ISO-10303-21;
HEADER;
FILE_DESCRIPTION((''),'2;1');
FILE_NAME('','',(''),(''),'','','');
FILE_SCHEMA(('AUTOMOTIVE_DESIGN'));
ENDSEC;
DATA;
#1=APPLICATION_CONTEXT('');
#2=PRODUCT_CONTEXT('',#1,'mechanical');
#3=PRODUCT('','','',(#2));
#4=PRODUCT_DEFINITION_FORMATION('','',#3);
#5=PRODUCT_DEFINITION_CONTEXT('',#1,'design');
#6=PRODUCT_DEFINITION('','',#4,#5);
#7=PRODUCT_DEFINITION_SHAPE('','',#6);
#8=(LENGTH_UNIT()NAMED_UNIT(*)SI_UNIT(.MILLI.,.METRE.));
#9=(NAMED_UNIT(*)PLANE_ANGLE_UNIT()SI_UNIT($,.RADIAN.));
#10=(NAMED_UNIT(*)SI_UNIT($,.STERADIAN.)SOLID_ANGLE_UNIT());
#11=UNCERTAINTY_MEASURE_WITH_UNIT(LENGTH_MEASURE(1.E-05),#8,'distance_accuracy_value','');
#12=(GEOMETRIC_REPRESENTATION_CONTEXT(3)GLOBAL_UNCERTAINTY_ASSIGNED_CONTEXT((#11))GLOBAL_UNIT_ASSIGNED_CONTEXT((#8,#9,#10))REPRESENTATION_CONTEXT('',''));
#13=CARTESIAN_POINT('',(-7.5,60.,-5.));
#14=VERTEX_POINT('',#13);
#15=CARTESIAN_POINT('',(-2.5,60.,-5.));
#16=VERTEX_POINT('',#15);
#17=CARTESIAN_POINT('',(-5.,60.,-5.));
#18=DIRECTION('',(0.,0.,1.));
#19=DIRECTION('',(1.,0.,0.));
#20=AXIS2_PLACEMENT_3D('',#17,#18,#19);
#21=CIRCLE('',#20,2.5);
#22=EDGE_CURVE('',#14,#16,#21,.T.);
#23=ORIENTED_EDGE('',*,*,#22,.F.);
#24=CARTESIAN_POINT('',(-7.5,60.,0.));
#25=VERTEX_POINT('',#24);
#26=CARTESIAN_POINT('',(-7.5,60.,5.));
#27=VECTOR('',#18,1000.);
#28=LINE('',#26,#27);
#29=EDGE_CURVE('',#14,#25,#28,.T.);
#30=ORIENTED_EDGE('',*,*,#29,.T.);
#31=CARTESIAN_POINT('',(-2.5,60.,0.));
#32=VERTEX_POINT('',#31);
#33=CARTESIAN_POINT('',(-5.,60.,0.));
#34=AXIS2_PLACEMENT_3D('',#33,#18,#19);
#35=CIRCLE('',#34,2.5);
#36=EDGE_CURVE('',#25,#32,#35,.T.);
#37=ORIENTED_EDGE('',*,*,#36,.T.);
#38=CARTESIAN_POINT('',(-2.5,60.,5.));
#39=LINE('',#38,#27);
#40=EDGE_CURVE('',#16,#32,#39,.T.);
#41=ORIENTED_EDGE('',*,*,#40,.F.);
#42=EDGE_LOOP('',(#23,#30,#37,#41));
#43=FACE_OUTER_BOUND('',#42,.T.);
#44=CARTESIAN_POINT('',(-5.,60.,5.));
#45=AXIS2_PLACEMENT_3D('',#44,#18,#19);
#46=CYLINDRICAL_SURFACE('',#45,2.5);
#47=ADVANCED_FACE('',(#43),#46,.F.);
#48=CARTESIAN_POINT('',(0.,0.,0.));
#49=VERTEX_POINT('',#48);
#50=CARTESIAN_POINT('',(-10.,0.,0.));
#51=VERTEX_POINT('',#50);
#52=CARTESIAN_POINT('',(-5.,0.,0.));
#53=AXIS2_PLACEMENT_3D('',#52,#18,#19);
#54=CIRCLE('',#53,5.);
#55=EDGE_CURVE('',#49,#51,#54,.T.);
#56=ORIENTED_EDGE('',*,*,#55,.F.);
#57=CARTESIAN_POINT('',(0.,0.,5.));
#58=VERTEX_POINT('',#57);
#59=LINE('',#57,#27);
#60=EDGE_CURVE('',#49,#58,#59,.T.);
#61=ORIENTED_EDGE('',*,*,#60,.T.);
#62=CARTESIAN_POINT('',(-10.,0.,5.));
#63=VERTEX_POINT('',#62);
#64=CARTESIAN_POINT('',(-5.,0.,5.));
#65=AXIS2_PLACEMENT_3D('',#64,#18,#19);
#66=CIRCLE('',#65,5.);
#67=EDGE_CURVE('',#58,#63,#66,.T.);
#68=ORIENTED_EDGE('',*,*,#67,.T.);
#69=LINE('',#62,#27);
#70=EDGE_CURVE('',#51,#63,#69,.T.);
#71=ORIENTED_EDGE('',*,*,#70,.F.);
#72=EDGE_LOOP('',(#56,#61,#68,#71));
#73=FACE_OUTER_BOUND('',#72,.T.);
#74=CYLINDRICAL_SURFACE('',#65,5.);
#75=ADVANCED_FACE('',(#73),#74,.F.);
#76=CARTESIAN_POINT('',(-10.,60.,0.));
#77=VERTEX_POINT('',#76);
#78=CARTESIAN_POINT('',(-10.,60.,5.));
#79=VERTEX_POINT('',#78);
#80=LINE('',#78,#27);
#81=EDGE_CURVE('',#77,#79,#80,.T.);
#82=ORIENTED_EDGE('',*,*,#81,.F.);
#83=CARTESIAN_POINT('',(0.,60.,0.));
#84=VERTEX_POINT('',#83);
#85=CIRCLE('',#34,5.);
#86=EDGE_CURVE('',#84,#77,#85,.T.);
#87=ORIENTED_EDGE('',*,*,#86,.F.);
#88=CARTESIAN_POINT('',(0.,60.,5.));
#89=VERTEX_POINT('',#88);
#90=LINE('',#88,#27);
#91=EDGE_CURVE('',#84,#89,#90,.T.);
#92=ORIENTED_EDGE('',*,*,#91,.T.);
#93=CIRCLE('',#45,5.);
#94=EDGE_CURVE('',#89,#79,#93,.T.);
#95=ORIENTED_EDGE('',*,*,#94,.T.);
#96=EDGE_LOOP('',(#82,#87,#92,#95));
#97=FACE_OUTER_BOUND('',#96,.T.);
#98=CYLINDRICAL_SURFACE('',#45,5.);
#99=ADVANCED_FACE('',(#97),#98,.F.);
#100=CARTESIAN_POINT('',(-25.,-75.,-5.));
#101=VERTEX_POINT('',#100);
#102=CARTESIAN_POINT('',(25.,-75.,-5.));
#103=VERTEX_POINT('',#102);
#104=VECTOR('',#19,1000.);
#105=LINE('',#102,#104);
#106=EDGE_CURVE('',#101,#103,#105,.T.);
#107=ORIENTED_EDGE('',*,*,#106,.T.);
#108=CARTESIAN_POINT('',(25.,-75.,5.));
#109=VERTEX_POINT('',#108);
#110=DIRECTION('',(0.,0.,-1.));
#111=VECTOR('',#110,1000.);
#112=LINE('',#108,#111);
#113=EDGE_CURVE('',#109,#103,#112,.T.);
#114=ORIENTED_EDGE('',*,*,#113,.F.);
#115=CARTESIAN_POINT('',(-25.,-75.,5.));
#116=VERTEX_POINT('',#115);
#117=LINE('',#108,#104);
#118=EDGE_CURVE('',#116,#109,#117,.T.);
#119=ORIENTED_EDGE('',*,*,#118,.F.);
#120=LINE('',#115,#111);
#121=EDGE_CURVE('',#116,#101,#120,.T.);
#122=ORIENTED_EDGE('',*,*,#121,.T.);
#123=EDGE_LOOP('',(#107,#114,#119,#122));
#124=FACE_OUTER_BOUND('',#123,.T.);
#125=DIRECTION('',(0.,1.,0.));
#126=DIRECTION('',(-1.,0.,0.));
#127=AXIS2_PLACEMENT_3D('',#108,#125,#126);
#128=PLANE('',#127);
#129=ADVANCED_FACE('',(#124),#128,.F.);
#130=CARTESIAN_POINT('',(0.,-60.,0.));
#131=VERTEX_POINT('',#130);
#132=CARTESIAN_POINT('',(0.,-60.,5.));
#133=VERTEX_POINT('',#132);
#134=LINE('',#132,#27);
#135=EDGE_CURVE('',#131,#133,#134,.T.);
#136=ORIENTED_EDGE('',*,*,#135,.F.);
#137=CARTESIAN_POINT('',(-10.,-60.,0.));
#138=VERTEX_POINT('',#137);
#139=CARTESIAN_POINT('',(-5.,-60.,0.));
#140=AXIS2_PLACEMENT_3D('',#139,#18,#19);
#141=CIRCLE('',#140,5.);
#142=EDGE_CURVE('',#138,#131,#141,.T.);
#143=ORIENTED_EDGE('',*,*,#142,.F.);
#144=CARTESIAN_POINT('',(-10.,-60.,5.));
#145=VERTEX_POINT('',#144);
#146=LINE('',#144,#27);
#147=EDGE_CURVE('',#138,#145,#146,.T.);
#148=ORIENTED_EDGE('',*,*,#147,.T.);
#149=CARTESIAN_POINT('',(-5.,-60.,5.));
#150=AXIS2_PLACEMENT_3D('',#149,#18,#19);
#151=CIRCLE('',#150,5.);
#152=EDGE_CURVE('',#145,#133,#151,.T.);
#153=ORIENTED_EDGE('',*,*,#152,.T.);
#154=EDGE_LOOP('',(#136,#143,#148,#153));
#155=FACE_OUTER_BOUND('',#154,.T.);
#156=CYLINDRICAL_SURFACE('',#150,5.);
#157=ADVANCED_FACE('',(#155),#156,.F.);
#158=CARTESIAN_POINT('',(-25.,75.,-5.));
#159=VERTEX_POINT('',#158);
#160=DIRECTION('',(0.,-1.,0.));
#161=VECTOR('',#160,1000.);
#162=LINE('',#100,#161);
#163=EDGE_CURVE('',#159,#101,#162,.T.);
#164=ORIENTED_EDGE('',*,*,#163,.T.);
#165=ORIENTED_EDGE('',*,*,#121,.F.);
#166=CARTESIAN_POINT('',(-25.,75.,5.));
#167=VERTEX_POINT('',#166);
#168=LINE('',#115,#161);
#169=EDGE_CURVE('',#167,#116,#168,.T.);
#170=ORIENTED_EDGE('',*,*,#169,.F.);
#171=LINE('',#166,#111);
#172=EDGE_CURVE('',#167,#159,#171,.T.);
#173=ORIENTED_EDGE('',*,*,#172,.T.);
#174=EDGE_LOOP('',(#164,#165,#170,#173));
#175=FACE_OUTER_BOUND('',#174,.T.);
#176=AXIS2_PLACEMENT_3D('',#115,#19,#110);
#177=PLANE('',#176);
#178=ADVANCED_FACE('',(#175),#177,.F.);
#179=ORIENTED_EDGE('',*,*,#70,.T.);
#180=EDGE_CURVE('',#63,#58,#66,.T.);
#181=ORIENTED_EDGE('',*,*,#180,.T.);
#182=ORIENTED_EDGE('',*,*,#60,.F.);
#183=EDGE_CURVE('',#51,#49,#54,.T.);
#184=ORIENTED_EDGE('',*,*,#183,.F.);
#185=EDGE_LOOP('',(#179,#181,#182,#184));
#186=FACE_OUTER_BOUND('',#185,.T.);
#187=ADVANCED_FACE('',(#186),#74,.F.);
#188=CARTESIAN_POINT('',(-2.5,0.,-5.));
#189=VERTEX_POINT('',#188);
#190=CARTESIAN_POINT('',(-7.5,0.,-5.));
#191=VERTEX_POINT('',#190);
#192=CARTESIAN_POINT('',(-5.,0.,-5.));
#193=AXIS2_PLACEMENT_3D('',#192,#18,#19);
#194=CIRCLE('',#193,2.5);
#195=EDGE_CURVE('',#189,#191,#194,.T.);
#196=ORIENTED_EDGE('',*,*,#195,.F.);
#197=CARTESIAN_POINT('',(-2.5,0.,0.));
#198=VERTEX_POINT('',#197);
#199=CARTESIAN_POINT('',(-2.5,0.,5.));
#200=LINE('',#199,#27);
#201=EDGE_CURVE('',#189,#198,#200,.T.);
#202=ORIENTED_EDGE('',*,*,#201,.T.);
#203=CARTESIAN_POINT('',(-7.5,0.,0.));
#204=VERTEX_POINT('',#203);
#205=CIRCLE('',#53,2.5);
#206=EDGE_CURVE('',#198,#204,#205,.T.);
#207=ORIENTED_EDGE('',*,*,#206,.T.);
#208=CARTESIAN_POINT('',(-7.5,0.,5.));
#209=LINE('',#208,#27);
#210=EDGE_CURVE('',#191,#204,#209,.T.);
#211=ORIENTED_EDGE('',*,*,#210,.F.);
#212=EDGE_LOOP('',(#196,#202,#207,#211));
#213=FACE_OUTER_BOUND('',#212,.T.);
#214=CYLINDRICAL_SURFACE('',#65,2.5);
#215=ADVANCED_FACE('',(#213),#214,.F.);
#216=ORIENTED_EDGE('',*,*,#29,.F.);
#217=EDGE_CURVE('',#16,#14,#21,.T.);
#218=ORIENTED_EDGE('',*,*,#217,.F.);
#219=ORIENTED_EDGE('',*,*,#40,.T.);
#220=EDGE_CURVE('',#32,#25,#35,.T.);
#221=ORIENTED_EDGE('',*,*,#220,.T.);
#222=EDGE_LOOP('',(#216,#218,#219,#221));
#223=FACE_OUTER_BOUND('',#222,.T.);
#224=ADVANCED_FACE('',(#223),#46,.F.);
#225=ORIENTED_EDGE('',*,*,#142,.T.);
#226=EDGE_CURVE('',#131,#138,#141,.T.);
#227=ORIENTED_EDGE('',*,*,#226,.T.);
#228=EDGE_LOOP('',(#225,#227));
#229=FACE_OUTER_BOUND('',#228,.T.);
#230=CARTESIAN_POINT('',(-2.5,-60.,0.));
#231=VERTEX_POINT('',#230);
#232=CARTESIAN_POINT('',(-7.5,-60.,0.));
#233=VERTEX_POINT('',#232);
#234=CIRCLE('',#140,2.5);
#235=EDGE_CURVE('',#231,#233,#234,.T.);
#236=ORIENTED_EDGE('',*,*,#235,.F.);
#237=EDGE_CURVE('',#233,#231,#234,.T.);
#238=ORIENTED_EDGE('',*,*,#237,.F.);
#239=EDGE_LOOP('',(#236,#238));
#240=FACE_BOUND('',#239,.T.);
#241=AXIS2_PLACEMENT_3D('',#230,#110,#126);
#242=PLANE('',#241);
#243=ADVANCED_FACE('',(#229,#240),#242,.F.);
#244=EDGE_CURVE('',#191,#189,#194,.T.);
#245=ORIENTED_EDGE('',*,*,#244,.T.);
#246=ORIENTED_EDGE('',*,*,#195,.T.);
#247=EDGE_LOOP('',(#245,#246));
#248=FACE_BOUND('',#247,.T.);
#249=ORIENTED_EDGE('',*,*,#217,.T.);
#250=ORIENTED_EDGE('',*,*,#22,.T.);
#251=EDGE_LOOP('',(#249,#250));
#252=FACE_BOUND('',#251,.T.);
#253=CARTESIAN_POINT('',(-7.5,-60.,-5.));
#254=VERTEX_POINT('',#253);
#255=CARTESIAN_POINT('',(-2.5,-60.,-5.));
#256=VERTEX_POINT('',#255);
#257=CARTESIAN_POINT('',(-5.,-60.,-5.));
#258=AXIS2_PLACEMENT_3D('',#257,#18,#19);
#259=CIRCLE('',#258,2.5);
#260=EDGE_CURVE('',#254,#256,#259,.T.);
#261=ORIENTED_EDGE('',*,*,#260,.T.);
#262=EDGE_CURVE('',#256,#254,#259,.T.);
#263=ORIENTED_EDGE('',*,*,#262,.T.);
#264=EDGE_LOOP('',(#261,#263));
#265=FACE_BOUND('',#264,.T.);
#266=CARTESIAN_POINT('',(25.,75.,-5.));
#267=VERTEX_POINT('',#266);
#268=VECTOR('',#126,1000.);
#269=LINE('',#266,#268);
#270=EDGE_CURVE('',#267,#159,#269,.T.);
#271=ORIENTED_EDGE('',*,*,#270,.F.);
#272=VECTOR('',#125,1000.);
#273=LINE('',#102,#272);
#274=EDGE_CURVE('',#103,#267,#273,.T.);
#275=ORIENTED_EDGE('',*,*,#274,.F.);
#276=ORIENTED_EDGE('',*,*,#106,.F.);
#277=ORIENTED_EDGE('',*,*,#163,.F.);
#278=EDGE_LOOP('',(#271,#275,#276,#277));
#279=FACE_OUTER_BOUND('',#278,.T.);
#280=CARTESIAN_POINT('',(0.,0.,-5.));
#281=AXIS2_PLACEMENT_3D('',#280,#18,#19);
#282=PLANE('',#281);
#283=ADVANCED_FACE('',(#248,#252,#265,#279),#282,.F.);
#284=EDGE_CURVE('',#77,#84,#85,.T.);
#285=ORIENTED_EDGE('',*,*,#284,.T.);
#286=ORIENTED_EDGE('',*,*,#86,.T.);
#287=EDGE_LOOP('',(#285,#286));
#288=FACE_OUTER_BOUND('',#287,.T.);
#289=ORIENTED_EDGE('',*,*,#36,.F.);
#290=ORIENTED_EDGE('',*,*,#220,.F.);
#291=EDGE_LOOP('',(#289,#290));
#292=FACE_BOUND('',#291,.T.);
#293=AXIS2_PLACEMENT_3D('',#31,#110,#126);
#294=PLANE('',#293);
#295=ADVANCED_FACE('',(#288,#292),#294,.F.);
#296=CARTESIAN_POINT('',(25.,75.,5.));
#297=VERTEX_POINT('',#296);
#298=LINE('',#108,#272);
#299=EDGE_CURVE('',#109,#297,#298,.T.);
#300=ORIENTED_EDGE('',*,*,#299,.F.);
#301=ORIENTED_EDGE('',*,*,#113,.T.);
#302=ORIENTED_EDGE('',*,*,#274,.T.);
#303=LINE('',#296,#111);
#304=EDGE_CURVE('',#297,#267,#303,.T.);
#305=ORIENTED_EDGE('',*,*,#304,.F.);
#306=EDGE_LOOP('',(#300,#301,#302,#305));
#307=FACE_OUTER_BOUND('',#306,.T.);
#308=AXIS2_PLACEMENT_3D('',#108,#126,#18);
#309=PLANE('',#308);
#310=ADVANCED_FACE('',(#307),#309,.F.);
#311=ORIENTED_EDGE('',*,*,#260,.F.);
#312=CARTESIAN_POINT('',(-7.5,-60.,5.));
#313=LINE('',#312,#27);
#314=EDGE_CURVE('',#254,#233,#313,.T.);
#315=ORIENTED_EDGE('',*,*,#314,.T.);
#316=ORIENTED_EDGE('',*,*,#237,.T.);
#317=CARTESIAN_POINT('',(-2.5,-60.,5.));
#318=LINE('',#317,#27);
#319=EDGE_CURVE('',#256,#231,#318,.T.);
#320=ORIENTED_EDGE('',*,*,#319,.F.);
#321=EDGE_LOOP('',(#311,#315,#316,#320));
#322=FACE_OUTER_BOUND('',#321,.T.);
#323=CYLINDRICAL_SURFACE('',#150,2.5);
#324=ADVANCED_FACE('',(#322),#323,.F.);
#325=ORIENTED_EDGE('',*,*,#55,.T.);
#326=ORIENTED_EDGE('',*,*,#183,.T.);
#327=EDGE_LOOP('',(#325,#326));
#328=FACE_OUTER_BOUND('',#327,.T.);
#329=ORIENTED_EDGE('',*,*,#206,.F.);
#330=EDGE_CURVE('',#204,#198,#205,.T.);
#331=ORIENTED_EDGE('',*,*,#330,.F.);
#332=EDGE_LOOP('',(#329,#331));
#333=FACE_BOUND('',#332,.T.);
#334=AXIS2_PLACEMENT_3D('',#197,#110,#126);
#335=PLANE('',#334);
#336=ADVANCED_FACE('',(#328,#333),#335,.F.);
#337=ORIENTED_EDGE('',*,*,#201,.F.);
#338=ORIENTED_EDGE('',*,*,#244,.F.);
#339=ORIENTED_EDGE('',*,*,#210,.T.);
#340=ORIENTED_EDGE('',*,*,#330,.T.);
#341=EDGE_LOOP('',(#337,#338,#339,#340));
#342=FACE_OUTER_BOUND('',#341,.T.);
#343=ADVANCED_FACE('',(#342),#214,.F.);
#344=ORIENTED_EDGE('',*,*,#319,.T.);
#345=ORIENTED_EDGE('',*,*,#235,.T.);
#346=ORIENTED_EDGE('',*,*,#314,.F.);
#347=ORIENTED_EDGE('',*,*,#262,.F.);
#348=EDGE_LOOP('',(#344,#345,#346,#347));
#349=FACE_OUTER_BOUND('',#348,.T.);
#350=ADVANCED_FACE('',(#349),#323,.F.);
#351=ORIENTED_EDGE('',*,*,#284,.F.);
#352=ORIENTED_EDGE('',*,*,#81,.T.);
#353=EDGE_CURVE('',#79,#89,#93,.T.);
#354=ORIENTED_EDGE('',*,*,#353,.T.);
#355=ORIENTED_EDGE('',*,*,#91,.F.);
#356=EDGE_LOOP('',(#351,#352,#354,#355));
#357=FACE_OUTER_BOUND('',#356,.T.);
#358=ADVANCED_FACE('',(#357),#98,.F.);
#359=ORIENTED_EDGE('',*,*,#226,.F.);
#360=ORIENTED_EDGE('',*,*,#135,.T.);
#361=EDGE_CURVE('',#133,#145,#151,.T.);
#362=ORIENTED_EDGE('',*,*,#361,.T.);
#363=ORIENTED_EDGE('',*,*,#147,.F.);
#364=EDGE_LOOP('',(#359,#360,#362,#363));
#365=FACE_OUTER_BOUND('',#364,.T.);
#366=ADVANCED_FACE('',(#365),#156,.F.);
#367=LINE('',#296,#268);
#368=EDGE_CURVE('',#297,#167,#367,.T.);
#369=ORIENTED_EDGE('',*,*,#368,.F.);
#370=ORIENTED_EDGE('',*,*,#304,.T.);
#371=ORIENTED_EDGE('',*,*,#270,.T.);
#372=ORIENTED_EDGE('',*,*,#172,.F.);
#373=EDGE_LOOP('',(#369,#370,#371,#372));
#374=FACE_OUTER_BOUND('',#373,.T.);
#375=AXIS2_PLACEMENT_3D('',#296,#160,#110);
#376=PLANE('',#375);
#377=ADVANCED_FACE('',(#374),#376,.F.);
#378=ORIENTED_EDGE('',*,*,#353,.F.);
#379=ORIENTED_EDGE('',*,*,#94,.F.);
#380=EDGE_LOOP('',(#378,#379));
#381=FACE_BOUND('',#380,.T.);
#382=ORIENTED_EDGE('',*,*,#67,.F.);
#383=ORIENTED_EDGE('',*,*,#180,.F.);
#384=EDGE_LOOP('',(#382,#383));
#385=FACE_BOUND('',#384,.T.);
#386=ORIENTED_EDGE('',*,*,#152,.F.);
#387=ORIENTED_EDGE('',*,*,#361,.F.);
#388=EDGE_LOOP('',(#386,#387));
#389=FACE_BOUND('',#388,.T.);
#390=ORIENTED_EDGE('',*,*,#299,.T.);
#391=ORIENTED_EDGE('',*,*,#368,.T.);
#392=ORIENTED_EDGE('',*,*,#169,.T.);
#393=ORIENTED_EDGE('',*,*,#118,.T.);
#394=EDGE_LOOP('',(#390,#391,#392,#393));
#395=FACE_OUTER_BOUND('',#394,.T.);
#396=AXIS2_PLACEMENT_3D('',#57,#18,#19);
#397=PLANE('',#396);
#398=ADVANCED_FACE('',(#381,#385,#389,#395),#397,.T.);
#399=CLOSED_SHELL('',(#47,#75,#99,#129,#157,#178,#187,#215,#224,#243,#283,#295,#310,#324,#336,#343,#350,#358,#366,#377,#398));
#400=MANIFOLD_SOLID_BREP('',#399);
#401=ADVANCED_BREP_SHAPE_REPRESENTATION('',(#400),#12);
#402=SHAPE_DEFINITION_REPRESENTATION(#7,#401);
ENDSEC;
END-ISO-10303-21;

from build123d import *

# Parameters (mm, degrees)
SKETCH1_W           = 50
SKETCH1_H           = 150
BOSS_EXTRUDE1_DEPTH = 5
HOLE1_D             = 5
HOLE1_CBORE_D       = 10
HOLE1_CBORE_DEPTH   = 5


with BuildPart() as part:
    # Sketch1 → Boss-Extrude1 (new, symmetric)
    with BuildSketch(Plane.XY):
        Rectangle(SKETCH1_W, SKETCH1_H)
    extrude(amount=BOSS_EXTRUDE1_DEPTH, both=True)

    # Hole1 (through all)
    with Locations(Plane.XY.offset(5)):
        with Locations((-5, 60), (-5, -60), (-5, 0)):
            CounterBoreHole(HOLE1_D / 2, HOLE1_CBORE_D / 2, HOLE1_CBORE_DEPTH)


solid = part.part
